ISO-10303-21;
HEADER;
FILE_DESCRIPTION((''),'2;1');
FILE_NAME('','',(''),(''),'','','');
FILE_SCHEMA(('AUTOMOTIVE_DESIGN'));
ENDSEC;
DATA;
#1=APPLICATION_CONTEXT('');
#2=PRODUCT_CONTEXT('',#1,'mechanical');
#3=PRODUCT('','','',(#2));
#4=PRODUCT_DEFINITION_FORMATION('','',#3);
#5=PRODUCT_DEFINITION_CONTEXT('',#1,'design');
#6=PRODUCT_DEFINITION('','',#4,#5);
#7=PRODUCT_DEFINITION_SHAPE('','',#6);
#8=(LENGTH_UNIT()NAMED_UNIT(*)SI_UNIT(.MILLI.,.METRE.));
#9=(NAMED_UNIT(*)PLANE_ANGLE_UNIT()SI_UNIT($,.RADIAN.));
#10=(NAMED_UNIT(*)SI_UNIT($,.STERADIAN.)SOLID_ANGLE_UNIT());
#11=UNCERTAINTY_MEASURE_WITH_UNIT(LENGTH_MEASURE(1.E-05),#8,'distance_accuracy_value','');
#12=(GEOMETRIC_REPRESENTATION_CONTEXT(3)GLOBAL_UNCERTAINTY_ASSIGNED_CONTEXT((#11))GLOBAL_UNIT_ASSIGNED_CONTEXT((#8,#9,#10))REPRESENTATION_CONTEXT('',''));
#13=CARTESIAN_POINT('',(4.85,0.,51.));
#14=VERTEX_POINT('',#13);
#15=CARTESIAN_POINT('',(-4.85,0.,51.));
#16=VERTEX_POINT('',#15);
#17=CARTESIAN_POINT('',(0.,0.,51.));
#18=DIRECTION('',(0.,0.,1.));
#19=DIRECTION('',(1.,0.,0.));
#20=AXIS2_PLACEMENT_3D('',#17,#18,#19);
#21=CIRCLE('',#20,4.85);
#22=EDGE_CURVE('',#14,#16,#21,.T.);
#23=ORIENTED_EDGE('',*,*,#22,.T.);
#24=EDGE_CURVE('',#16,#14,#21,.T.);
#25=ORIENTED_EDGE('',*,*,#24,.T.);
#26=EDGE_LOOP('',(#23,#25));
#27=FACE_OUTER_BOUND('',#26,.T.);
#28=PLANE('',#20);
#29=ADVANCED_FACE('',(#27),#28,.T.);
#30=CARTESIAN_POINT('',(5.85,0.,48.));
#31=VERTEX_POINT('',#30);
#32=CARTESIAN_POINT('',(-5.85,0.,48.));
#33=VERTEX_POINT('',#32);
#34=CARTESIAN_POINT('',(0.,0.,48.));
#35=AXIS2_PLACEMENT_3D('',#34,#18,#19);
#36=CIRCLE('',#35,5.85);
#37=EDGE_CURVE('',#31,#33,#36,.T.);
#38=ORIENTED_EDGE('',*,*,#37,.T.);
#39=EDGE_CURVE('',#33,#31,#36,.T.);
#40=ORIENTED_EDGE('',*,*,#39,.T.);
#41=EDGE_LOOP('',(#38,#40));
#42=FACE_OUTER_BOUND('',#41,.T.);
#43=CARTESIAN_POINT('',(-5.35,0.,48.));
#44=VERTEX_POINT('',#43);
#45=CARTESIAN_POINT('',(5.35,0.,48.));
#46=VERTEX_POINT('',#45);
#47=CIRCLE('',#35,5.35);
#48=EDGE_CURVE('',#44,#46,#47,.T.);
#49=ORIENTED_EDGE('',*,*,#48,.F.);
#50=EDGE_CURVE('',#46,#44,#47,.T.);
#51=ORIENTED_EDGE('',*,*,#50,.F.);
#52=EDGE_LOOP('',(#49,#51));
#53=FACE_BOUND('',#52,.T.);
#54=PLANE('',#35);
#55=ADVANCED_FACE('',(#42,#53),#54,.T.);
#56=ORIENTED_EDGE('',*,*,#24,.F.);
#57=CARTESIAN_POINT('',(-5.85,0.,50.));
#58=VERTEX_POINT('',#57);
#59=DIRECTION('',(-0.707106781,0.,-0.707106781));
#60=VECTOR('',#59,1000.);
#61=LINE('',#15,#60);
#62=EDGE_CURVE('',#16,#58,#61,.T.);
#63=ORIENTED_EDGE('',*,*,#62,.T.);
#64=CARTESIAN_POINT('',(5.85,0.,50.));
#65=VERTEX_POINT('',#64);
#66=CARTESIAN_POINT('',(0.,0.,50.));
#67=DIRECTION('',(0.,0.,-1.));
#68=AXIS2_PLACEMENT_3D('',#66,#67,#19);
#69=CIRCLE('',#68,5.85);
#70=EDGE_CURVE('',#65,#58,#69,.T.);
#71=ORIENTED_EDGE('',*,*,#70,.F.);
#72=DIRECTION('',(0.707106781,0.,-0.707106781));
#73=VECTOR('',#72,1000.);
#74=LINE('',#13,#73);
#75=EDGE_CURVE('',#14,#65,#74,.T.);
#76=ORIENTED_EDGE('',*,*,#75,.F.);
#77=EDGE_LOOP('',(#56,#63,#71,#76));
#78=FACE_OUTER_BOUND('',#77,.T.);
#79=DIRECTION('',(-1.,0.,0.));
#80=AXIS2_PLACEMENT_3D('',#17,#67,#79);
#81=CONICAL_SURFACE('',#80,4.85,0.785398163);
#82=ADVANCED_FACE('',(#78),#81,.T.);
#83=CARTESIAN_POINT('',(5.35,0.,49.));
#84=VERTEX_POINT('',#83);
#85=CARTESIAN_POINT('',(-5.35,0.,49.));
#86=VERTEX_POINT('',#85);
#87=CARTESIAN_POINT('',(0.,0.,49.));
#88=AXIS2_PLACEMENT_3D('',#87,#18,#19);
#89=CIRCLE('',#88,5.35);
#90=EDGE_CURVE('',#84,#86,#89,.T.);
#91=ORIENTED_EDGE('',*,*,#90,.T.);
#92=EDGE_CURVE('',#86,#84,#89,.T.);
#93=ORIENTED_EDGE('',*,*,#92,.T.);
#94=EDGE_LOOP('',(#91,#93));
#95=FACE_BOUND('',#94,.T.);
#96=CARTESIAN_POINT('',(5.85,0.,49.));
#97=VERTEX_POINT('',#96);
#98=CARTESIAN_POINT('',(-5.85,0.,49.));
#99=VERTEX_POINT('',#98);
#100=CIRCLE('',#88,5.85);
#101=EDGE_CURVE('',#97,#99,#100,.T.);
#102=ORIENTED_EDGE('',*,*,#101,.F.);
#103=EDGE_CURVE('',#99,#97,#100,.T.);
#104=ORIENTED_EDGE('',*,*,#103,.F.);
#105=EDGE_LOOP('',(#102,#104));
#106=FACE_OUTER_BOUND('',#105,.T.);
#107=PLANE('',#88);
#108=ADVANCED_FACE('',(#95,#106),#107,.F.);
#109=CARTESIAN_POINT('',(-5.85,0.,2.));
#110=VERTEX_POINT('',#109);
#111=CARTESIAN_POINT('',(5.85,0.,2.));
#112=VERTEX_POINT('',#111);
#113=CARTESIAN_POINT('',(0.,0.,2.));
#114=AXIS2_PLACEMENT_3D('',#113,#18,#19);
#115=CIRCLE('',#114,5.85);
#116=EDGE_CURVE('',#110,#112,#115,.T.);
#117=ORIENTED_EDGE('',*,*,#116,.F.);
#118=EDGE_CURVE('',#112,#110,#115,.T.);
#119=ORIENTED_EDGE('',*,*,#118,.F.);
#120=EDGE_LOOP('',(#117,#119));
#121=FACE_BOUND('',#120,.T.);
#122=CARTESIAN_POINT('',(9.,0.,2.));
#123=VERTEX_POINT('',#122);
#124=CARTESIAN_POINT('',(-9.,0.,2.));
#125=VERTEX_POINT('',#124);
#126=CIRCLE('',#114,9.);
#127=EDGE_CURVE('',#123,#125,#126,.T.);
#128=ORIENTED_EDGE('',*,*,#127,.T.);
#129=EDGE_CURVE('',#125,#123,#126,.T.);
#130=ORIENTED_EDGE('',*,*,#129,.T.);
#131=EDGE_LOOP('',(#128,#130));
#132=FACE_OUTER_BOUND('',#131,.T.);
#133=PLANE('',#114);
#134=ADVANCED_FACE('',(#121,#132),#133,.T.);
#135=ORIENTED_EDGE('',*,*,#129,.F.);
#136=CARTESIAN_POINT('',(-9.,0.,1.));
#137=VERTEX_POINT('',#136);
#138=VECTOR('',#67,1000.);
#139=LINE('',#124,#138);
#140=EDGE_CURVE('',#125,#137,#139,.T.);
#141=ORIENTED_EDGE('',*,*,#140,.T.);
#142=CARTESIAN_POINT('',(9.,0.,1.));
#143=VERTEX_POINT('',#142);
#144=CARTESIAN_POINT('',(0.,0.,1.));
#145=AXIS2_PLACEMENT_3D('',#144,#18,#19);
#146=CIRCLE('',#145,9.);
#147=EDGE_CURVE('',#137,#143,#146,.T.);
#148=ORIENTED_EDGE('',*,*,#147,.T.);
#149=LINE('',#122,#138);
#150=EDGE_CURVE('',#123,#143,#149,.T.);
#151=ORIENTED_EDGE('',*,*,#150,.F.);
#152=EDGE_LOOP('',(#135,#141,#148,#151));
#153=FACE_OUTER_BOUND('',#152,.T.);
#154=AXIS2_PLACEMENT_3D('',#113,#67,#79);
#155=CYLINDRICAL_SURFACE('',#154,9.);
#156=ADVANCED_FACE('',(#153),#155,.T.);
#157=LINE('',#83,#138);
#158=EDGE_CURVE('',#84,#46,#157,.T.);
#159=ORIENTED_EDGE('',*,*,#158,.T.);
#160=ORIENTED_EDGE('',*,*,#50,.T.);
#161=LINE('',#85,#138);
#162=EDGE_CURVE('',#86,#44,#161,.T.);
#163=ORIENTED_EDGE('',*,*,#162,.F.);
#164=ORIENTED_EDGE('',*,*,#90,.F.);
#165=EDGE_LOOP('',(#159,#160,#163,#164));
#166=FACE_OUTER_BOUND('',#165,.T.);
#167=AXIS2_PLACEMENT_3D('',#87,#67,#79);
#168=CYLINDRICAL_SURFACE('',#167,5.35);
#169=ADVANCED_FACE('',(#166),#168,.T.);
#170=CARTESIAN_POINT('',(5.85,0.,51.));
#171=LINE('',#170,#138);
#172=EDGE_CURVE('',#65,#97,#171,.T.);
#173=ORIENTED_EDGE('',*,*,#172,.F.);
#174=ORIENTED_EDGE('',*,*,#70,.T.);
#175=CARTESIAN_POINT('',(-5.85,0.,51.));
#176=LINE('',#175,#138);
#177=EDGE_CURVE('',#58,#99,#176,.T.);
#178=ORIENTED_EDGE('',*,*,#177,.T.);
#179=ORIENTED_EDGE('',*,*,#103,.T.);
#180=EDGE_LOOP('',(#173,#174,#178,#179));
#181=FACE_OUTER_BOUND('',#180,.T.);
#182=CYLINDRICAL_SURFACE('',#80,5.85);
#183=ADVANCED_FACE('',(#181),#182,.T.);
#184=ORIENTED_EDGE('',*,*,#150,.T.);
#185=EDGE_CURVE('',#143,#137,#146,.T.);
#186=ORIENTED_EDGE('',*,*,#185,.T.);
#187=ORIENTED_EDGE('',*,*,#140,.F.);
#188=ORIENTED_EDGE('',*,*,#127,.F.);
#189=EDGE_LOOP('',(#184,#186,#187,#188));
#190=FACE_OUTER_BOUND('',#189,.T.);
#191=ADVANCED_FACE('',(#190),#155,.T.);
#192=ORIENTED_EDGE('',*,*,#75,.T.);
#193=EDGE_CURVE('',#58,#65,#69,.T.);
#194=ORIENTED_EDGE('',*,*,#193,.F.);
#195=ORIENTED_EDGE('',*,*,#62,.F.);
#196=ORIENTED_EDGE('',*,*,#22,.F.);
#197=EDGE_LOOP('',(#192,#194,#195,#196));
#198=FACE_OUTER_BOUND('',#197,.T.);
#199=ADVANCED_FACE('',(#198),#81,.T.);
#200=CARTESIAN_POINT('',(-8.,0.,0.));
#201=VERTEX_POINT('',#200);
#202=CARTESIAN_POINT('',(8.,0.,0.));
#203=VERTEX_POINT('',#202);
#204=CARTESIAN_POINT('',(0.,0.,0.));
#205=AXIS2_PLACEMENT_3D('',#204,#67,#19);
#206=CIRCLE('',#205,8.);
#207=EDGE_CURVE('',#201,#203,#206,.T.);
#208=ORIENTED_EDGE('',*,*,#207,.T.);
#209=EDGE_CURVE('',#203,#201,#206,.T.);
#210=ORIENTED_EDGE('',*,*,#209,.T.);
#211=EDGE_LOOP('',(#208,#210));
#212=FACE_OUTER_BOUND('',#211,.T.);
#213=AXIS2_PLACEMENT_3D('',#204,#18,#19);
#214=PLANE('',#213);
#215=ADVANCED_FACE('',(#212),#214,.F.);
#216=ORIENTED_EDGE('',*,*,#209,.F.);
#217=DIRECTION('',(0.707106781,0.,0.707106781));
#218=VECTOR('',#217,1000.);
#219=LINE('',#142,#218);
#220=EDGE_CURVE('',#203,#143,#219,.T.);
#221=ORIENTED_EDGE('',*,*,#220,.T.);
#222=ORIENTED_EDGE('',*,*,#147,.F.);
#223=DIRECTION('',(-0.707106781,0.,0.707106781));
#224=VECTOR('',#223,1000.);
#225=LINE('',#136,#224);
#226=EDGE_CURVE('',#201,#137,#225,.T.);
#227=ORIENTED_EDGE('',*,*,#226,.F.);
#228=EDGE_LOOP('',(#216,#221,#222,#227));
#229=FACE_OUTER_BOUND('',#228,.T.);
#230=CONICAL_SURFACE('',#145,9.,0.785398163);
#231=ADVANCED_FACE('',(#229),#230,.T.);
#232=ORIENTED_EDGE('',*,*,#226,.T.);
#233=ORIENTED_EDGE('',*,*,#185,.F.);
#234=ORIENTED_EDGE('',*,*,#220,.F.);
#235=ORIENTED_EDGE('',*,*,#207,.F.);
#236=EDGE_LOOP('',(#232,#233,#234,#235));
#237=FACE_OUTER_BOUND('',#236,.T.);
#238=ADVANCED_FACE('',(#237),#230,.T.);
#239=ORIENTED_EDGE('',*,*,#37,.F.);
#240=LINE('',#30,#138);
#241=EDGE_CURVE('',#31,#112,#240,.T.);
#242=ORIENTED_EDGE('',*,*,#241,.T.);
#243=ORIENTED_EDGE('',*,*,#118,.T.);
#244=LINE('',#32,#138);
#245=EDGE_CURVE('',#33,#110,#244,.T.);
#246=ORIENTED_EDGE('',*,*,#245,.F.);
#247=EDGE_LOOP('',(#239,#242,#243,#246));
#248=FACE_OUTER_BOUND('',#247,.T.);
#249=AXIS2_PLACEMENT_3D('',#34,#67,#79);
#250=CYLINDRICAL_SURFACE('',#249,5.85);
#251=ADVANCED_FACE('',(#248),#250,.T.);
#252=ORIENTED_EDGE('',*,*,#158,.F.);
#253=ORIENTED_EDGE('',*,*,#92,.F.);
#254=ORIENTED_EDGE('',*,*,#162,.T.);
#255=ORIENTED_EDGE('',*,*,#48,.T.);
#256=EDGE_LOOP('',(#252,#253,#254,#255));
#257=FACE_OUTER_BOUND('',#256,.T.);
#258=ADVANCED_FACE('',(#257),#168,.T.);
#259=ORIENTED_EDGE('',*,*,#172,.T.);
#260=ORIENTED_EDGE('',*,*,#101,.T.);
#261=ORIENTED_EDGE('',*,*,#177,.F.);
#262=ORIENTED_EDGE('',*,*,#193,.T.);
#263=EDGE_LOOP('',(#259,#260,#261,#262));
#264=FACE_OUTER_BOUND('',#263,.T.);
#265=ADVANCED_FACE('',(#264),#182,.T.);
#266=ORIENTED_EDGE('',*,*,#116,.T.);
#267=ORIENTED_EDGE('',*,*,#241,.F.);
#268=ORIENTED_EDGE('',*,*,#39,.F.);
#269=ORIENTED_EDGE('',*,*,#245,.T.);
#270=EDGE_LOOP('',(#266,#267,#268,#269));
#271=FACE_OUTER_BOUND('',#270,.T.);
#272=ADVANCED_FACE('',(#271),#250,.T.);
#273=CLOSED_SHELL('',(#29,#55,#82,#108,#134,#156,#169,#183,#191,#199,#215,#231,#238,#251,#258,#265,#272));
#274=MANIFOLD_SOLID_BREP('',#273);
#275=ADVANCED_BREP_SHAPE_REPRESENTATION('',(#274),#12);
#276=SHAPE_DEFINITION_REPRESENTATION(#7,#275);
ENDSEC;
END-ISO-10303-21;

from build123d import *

# Parameters (mm, degrees)
SKETCH1_R           = 9
BOSS_EXTRUDE1_DEPTH = 2
SKETCH2_R           = 5.85
BOSS_EXTRUDE2_DEPTH = 46
SKETCH4_R           = 5.35
BOSS_EXTRUDE3_DEPTH = 1
SKETCH5_R           = 5.85
BOSS_EXTRUDE4_DEPTH = 2
CHAMFER1_SIZE       = 1


with BuildPart() as part:
    # Sketch1 → Boss-Extrude1 (new body)
    with BuildSketch(Plane.XY):
        Circle(SKETCH1_R)
    extrude(amount=BOSS_EXTRUDE1_DEPTH)

    # Sketch2 → Boss-Extrude2 (add)
    with BuildSketch(Plane.XY.offset(2)):
        Circle(SKETCH2_R)
    extrude(amount=BOSS_EXTRUDE2_DEPTH)

    # Sketch4 → Boss-Extrude3 (add)
    with BuildSketch(Plane.XY.offset(48)):
        Circle(SKETCH4_R)
    extrude(amount=BOSS_EXTRUDE3_DEPTH)

    # Sketch5 → Boss-Extrude4 (add)
    with BuildSketch(Plane.XY.offset(49)):
        Circle(SKETCH5_R)
    extrude(amount=BOSS_EXTRUDE4_DEPTH)

    # Chamfer1
    chamfer1_edges = [part.edges().sort_by_distance(p)[0] for p in [
        (-5.85, 0, 51),
        (-9, 0, 0),
    ]]
    chamfer(chamfer1_edges, length=CHAMFER1_SIZE)


solid = part.part
